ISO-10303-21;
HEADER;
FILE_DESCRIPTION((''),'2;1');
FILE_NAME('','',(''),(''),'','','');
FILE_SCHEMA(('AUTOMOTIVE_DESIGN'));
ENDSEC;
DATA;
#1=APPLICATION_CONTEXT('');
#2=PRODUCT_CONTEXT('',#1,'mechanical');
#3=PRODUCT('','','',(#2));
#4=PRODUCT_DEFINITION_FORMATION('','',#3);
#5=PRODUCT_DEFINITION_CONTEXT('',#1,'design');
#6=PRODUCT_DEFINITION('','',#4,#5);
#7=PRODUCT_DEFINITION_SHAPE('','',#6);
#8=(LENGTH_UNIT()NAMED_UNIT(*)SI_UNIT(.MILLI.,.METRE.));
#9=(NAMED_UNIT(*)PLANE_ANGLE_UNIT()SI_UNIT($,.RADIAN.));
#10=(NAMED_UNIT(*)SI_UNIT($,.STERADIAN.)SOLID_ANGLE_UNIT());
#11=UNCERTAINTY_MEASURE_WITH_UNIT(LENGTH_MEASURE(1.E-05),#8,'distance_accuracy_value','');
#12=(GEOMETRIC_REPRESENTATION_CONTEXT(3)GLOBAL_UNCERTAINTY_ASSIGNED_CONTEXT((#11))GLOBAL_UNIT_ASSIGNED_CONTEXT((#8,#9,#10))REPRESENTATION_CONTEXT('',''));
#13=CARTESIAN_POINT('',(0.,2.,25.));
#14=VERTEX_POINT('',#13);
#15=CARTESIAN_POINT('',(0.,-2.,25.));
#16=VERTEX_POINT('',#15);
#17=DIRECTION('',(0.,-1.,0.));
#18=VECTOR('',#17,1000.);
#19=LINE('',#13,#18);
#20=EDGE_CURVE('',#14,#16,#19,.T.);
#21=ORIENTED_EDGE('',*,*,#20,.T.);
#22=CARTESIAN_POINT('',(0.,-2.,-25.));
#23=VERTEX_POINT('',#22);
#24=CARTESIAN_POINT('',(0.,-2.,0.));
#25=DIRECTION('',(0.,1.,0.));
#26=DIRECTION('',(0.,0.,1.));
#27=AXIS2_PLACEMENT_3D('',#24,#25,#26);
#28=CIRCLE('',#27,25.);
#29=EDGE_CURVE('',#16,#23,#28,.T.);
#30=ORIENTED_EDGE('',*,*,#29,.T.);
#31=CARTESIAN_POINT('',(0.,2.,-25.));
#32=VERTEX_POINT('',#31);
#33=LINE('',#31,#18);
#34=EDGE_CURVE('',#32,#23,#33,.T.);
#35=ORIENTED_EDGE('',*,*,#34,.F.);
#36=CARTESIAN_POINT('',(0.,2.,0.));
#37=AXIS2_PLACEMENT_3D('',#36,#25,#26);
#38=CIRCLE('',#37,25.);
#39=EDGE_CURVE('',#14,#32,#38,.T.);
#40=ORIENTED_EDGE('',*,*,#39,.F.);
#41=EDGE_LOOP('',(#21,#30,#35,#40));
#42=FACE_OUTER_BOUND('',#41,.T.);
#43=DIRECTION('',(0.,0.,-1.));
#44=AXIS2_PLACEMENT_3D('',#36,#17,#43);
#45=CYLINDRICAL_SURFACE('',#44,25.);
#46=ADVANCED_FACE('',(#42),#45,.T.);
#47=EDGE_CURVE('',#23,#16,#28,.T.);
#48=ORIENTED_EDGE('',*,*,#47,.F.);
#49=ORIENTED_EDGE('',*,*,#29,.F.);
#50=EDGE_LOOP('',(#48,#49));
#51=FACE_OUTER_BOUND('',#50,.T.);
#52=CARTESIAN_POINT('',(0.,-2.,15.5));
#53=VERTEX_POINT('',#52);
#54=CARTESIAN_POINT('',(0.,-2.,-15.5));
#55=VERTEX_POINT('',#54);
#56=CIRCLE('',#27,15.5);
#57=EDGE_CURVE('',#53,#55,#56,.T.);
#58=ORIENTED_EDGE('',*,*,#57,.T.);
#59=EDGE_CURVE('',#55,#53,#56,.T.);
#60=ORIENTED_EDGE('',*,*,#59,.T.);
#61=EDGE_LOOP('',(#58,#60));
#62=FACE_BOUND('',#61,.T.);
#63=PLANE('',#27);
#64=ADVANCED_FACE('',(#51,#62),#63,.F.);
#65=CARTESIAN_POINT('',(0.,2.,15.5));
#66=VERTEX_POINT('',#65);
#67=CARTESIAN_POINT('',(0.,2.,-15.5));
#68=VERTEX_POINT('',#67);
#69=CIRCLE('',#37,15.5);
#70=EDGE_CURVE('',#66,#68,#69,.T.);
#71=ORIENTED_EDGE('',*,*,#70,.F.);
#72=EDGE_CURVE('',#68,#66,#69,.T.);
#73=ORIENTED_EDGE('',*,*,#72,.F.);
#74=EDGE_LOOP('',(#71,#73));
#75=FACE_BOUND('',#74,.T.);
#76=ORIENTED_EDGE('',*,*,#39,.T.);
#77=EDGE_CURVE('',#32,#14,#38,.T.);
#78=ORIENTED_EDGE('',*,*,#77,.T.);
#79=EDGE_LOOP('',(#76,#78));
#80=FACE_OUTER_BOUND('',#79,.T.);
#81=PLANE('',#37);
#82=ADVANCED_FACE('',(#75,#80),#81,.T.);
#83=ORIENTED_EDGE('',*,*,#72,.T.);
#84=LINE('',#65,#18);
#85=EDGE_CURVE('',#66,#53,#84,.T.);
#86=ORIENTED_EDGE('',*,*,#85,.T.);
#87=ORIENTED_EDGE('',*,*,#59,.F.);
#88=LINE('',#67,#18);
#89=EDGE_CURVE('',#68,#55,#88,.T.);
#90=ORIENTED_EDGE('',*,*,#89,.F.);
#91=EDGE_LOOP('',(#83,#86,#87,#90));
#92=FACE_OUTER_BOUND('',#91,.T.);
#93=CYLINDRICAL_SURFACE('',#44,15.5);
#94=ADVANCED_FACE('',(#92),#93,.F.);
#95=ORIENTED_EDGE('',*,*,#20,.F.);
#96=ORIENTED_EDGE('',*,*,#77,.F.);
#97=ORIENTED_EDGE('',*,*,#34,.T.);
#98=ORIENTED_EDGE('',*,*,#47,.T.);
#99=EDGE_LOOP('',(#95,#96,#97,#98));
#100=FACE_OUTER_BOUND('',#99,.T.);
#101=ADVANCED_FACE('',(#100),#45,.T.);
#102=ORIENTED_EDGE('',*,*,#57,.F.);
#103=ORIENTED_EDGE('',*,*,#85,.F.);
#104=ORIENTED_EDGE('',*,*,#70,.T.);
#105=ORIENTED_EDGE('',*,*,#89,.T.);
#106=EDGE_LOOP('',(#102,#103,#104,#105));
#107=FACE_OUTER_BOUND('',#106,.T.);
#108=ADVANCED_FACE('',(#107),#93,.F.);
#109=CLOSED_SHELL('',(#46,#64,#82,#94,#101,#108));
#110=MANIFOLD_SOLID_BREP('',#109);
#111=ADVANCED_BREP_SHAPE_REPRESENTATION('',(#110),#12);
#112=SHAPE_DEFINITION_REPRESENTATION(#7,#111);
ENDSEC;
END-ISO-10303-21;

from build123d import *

# Parameters (mm, degrees)
SKETCH_1_R      = 25
SKETCH_1_R_2    = 15.5
EXTRUDE_1_DEPTH = 2


with BuildPart() as part:
    # 草图1 → 凸台-拉伸1 (new, symmetric)
    with BuildSketch(Plane(origin=(0, 0, 0), x_dir=(1, 0, 0), z_dir=(0, 1, 0))):
        with Locations(Location((0, 0, 0), (0, 0, 270))):
            Circle(SKETCH_1_R)
        with Locations(Location((0, 0, 0), (0, 0, 270))):
            Circle(SKETCH_1_R_2, mode=Mode.SUBTRACT)
    extrude(amount=EXTRUDE_1_DEPTH, both=True)


solid = part.part
